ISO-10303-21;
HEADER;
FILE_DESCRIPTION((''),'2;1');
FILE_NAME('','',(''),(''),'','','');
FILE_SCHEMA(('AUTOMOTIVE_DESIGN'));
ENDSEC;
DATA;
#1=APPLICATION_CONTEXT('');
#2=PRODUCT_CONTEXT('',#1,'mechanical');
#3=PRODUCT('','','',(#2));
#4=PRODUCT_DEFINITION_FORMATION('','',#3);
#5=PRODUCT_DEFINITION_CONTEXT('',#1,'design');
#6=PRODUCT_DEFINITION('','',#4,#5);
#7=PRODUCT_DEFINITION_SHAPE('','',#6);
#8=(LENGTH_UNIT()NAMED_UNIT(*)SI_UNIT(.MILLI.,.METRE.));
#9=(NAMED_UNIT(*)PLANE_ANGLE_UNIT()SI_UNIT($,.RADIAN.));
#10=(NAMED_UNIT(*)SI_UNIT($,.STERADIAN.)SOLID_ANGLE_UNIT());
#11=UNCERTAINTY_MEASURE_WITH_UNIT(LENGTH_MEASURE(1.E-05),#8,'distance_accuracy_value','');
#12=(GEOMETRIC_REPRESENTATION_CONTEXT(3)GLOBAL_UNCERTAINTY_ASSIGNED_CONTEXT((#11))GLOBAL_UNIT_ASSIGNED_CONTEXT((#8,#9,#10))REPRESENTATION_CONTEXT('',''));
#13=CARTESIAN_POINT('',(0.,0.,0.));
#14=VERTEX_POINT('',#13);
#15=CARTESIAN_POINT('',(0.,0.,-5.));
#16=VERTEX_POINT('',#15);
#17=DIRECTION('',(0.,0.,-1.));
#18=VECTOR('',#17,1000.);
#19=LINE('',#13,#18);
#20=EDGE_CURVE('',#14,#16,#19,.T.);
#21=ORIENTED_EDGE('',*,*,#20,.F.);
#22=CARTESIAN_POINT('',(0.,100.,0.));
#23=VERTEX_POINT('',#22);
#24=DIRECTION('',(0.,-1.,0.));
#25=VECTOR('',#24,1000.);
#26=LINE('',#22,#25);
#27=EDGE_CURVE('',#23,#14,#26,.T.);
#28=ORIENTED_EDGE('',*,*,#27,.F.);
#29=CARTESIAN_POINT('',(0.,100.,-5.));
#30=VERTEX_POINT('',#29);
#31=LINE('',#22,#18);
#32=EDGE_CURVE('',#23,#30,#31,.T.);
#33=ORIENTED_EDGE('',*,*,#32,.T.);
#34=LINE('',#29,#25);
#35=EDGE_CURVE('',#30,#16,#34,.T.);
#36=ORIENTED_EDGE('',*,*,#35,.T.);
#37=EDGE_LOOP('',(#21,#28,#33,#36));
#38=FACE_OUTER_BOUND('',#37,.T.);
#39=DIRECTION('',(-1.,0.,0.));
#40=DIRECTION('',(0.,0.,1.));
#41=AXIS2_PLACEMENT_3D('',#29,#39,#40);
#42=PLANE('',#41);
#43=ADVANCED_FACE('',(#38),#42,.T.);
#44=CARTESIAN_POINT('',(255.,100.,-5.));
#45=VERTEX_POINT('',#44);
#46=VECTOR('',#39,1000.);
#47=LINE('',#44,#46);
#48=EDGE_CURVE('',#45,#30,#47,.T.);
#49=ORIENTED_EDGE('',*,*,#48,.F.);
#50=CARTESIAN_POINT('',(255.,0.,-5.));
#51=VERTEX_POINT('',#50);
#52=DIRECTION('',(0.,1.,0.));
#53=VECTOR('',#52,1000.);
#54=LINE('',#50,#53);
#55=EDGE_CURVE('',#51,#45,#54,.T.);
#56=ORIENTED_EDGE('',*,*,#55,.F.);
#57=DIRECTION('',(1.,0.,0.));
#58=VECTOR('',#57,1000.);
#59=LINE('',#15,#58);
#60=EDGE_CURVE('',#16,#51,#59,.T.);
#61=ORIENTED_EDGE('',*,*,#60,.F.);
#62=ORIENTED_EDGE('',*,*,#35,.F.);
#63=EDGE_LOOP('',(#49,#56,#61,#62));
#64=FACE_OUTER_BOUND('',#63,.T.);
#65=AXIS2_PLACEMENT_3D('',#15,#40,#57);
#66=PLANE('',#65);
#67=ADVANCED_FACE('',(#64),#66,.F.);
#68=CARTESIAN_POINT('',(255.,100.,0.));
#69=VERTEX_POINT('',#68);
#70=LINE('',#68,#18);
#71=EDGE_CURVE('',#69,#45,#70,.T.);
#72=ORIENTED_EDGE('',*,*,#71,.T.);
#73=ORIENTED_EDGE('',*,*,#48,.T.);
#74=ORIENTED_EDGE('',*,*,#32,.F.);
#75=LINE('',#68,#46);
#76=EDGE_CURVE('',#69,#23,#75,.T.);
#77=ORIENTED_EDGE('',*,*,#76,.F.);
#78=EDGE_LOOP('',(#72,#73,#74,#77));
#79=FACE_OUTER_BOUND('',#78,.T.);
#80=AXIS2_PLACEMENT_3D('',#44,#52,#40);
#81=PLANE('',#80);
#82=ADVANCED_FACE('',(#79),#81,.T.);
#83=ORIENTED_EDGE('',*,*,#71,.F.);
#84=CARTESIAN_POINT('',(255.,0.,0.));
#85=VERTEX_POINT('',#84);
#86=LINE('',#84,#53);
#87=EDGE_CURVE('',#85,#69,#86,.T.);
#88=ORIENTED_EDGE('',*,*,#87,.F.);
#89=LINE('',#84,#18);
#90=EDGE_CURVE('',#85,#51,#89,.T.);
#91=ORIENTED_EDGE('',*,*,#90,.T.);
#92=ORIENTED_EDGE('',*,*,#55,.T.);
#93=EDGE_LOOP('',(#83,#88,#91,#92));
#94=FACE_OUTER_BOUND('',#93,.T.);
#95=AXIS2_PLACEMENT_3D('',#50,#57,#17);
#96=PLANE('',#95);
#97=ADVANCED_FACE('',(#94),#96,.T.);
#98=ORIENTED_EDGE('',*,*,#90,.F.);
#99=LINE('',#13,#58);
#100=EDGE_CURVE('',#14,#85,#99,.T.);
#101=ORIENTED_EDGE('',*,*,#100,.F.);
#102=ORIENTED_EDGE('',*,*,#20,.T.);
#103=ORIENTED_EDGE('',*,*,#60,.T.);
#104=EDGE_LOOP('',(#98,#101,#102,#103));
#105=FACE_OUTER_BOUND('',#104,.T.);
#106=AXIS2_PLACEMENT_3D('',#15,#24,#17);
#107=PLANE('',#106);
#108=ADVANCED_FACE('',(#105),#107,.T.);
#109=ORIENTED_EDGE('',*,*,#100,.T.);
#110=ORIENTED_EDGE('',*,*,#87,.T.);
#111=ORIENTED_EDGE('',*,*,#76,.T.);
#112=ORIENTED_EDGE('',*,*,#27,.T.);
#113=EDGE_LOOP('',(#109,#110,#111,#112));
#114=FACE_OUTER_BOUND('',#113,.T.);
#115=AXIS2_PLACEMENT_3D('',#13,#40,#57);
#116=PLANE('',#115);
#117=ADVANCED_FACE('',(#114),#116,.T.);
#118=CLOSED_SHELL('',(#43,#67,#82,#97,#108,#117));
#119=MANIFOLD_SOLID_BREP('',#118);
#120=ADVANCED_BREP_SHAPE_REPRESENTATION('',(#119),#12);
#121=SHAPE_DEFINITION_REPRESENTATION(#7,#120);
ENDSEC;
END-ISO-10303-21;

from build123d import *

# Parameters (mm, degrees)
SKETCH_2_W          = 255
SKETCH_2_H          = 100
EXTRUDE_1_DEPTH     = 5
CUT_EXTRUDE_1_DEPTH = 5
CUT_EXTRUDE_2_DEPTH = 21
EXTRUDE_2_DEPTH     = 5


with BuildPart() as part:
    # 草图2 → 凸台-拉伸1 (new body)
    with BuildSketch(Plane.XY):
        with Locations((127.5, 50)):
            Rectangle(SKETCH_2_W, SKETCH_2_H)
    extrude(amount=-EXTRUDE_1_DEPTH)

    # 草图3 → 切除-拉伸1 (cut)
    with BuildSketch(Plane.XY):
        Polygon((0, 100), (10, 100), (0, 90), align=None)
        Polygon((255, 100), (245, 100), (255, 90), align=None)
        Polygon((255, 0), (255, 10), (245, 0), align=None)
        Polygon((0, 0), (0, 10), (10, 0), align=None)
    extrude(amount=-CUT_EXTRUDE_1_DEPTH, mode=Mode.SUBTRACT)

    # 草图4 → 切除-拉伸2 (cut)
    with BuildSketch(Plane(origin=(0, 0, -5), x_dir=(-1, 0, 0), z_dir=(0, 0, -1))):
        with BuildLine():
            ThreePointArc((-242, 83.5), (-248.5, 90), (-242, 96.5))
            Line((-242, 96.5), (-215, 96.5))
            ThreePointArc((-215, 96.5), (-208.5, 90), (-215, 83.5))
            Line((-215, 83.5), (-242, 83.5))
        make_face()
        with BuildLine():
            Line((-40, 96.5), (-13, 96.5))
            ThreePointArc((-13, 96.5), (-6.5, 90), (-13, 83.5))
            Line((-13, 83.5), (-40, 83.5))
            ThreePointArc((-40, 83.5), (-46.5, 90), (-40, 96.5))
        make_face()
        with BuildLine():
            ThreePointArc((-13, 16.5), (-6.5, 10), (-13, 3.5))
            Line((-13, 3.5), (-40, 3.5))
            ThreePointArc((-40, 3.5), (-46.5, 10), (-40, 16.5))
            Line((-40, 16.5), (-13, 16.5))
        make_face()
        with BuildLine():
            Line((-215, 3.5), (-242, 3.5))
            ThreePointArc((-242, 3.5), (-248.5, 10), (-242, 16.5))
            Line((-242, 16.5), (-215, 16.5))
            ThreePointArc((-215, 16.5), (-208.5, 10), (-215, 3.5))
        make_face()
    extrude(amount=-CUT_EXTRUDE_2_DEPTH, mode=Mode.SUBTRACT)

    # 草图5 → 凸台-拉伸2 (add)
    with BuildSketch(Plane(origin=(0, 0, -5), x_dir=(-1, 0, 0), z_dir=(0, 0, -1))):
        Polygon((-255, 90), (-255, 100), (0, 100), (0, 0), (-255, 0), align=None)
    extrude(amount=-EXTRUDE_2_DEPTH)


solid = part.part
